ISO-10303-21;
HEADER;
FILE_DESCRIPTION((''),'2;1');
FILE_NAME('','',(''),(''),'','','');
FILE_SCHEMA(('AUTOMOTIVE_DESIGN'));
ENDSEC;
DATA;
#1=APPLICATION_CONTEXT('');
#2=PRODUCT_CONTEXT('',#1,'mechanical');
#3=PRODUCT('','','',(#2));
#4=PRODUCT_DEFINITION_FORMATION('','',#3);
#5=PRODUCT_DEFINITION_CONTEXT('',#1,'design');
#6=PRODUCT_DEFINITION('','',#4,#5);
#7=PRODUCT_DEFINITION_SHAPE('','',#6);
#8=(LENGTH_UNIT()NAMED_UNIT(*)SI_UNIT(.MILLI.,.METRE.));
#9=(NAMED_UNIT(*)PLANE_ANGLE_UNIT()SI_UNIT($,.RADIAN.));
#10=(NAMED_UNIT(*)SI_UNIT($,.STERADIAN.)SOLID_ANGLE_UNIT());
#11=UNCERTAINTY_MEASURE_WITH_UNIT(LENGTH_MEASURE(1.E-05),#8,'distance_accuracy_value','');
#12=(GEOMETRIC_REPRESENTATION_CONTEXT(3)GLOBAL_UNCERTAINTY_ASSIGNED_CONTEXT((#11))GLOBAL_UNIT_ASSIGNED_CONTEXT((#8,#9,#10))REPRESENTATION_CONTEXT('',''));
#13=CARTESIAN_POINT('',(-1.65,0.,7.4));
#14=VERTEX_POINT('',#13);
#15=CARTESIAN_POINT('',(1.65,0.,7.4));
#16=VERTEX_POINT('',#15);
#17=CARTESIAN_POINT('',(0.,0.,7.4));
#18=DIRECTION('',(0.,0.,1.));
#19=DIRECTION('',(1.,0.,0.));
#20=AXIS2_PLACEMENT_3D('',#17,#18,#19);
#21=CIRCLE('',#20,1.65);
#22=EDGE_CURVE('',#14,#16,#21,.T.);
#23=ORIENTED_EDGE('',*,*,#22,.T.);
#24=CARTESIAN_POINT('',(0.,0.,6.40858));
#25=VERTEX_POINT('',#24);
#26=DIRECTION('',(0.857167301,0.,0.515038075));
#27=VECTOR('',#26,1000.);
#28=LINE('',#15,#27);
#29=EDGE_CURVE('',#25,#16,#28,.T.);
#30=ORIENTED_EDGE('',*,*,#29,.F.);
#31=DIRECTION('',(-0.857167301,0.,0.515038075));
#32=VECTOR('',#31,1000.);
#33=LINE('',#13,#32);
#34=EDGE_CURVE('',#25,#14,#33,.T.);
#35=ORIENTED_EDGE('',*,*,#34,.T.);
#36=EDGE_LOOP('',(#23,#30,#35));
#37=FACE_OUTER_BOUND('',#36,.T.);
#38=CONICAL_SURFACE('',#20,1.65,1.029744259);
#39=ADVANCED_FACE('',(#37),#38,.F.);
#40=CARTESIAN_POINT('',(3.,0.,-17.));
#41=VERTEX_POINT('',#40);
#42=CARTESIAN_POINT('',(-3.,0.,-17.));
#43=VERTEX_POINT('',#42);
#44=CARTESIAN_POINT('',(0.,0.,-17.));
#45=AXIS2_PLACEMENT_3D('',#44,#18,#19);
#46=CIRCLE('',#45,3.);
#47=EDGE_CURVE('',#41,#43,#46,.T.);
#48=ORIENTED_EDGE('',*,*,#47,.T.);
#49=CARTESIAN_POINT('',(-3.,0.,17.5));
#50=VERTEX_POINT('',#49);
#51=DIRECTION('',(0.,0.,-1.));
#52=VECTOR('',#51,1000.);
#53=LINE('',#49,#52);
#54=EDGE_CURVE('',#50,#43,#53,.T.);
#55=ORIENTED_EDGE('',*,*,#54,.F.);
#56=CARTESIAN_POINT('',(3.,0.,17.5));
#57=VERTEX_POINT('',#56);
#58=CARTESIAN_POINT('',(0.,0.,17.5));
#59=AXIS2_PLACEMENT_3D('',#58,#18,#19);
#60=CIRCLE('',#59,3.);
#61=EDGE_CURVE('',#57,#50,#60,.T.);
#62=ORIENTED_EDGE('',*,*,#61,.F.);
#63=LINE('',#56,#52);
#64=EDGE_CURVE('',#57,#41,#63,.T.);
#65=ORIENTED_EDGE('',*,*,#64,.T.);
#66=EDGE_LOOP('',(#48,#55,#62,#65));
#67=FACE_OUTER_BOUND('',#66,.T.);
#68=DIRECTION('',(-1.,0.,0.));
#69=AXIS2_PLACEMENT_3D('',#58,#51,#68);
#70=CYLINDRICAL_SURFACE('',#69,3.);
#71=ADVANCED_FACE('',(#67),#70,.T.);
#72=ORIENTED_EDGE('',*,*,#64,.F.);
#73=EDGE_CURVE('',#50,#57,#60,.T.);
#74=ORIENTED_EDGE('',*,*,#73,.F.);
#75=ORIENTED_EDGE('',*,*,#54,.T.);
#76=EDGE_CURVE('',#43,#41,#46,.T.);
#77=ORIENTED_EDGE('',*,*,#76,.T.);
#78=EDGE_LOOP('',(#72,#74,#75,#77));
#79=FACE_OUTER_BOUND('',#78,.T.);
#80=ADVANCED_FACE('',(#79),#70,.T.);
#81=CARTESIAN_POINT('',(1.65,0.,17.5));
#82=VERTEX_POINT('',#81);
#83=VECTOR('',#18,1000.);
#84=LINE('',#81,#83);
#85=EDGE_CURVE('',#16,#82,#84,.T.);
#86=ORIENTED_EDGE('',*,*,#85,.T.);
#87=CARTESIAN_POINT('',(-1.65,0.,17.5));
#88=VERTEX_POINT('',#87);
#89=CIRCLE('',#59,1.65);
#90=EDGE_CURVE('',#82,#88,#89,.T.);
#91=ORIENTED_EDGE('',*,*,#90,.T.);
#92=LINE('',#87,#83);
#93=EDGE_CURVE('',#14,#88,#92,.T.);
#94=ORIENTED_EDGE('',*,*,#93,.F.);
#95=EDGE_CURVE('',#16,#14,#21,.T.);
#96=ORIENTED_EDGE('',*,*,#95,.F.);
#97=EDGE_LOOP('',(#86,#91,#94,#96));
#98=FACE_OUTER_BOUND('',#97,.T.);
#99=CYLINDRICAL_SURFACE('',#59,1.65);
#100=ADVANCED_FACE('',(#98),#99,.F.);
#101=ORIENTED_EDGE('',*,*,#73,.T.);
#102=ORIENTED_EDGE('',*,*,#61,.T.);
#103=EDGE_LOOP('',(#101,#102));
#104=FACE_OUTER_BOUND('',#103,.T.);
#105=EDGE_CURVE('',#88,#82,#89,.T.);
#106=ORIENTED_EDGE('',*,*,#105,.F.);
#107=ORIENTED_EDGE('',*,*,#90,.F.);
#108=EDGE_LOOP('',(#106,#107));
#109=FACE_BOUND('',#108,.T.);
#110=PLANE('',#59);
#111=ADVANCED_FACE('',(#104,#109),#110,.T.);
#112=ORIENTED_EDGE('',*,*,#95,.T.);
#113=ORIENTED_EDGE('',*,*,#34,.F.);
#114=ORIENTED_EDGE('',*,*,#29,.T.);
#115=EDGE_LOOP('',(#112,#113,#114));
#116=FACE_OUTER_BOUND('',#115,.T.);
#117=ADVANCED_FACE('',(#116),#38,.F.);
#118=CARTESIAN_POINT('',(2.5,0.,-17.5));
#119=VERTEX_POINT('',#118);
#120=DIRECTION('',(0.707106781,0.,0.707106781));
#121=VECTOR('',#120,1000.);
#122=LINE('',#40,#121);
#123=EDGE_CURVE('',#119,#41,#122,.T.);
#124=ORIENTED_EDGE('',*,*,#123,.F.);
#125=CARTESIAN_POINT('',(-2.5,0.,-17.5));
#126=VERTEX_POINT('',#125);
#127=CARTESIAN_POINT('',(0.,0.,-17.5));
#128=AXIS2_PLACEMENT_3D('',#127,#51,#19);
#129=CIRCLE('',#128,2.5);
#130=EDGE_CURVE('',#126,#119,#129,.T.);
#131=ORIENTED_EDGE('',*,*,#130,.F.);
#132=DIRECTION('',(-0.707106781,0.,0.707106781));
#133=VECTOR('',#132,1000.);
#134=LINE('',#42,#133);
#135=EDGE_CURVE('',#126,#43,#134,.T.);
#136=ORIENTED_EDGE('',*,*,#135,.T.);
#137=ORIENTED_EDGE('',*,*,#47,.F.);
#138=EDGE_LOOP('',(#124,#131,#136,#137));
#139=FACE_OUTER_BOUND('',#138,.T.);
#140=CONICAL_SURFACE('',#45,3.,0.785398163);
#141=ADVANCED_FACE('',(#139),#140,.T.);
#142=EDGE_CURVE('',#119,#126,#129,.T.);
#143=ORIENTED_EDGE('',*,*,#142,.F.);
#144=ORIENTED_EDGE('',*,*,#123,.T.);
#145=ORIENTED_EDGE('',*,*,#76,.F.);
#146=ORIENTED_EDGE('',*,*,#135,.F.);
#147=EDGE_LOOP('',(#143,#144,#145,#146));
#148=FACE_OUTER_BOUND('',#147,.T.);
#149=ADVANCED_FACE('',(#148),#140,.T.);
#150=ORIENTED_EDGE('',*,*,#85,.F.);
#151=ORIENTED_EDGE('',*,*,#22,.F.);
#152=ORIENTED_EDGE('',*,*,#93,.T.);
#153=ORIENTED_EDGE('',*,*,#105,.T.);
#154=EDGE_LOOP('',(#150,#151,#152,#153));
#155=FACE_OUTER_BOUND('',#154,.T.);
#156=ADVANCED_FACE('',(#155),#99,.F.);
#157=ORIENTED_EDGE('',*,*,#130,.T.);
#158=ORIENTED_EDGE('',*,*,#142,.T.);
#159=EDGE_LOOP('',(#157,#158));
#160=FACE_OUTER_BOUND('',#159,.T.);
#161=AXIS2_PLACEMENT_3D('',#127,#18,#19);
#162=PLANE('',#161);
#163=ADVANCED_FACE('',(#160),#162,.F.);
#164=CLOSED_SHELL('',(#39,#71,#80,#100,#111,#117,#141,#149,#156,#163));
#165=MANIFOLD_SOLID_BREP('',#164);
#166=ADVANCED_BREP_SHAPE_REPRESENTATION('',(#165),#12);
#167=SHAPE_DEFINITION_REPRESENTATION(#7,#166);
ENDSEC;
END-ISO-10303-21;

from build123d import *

# Parameters (mm, degrees)
SKETCH1_R             = 3
BOSS_EXTRUDE1_DEPTH   = 17.5
M4_TAPPED_HOLE1_D     = 3.3
M4_TAPPED_HOLE1_DEPTH = 10.1
M4_TAPPED_HOLE1_TIP   = 0.991420021
CHAMFER1_SIZE         = 0.5


with BuildPart() as part:
    # Sketch1 → Boss-Extrude1 (new, symmetric)
    with BuildSketch(Plane.XY):
        Circle(SKETCH1_R)
    extrude(amount=BOSS_EXTRUDE1_DEPTH, both=True)

    # M4 Tapped Hole1
    with Locations(Plane.XY.offset(17.5)):
        with Locations((0, 0)):
            Hole(M4_TAPPED_HOLE1_D / 2, depth=M4_TAPPED_HOLE1_DEPTH)
            with Locations((0, 0, -(M4_TAPPED_HOLE1_DEPTH + M4_TAPPED_HOLE1_TIP / 2))):  # 118° drill point
                Cone(0, M4_TAPPED_HOLE1_D / 2, M4_TAPPED_HOLE1_TIP, mode=Mode.SUBTRACT)

    # Chamfer1
    chamfer1_edges = [part.edges().sort_by_distance(p)[0] for p in [
        (-3, 0, -17.5),
    ]]
    chamfer(chamfer1_edges, length=CHAMFER1_SIZE)


solid = part.part
